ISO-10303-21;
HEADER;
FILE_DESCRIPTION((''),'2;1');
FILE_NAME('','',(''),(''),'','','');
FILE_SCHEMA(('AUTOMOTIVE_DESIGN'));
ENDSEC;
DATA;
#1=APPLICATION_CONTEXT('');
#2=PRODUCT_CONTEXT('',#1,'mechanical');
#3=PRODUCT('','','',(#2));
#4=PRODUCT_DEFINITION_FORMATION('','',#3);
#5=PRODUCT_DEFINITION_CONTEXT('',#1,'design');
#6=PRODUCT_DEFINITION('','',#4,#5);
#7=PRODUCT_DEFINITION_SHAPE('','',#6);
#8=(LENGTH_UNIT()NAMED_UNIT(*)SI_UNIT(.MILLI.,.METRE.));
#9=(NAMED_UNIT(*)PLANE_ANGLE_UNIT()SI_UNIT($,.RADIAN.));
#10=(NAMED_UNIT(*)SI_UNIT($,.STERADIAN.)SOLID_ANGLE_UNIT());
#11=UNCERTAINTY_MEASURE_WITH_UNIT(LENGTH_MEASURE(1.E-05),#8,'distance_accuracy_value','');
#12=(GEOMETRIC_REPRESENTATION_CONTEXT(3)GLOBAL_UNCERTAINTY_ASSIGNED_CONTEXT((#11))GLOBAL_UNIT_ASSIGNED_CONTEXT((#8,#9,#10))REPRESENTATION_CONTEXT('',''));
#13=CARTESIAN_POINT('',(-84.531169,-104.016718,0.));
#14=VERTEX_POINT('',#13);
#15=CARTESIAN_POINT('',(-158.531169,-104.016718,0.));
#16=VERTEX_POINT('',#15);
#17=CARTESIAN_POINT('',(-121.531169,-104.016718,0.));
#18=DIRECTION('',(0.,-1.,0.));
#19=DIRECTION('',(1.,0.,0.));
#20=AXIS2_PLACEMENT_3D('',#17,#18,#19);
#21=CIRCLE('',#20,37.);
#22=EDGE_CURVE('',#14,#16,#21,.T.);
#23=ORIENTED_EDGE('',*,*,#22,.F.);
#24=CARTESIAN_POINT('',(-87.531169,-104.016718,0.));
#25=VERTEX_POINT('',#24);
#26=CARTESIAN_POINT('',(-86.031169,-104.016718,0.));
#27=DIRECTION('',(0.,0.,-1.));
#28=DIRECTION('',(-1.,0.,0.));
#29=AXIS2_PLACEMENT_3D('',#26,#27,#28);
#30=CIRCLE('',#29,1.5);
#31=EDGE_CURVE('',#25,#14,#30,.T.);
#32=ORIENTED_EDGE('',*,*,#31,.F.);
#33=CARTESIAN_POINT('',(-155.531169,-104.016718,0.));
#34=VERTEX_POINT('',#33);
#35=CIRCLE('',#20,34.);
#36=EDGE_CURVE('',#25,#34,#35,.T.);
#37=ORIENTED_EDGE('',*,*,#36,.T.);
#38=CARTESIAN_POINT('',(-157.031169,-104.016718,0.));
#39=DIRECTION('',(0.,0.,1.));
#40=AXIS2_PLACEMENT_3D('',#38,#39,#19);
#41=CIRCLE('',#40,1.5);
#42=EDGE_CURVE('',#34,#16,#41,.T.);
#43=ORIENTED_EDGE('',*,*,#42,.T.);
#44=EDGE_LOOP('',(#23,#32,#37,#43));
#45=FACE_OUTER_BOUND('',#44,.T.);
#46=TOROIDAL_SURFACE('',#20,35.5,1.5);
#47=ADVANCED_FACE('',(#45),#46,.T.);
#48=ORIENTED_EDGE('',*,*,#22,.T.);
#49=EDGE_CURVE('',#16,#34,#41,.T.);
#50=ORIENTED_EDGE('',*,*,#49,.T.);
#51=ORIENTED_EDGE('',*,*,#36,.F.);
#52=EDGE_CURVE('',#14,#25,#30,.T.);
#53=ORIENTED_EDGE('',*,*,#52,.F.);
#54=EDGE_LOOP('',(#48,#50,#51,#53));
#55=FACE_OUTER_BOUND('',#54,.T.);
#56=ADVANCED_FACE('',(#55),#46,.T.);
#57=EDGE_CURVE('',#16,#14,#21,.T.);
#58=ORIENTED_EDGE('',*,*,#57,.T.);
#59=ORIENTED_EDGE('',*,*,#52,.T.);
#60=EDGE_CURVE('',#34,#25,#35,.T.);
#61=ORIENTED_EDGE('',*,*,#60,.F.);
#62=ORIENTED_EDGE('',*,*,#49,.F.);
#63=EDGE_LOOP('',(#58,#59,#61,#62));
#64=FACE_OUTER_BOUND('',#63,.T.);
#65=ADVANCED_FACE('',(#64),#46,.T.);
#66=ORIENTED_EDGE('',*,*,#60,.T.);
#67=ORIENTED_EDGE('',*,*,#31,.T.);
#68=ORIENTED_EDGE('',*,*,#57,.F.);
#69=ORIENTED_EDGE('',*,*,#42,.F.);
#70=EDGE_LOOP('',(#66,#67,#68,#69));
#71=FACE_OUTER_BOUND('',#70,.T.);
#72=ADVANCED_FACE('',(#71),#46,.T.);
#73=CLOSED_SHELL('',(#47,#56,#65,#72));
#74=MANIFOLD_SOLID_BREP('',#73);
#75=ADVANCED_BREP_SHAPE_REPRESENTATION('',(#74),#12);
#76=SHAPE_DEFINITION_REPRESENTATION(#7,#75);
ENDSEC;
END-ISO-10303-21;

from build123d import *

# Parameters (mm, degrees)
SKETCH1_R = 1.5


with BuildPart() as part:
    # Sketch1 → Revolve1 (revolve)
    with BuildSketch(Plane.XY):
        with Locations((-86.031169153, -104.0167177)):
            Circle(SKETCH1_R)
    revolve(axis=Axis((-121.531169153, -142.3167177, 0), (0, 1, 0)))


solid = part.part
